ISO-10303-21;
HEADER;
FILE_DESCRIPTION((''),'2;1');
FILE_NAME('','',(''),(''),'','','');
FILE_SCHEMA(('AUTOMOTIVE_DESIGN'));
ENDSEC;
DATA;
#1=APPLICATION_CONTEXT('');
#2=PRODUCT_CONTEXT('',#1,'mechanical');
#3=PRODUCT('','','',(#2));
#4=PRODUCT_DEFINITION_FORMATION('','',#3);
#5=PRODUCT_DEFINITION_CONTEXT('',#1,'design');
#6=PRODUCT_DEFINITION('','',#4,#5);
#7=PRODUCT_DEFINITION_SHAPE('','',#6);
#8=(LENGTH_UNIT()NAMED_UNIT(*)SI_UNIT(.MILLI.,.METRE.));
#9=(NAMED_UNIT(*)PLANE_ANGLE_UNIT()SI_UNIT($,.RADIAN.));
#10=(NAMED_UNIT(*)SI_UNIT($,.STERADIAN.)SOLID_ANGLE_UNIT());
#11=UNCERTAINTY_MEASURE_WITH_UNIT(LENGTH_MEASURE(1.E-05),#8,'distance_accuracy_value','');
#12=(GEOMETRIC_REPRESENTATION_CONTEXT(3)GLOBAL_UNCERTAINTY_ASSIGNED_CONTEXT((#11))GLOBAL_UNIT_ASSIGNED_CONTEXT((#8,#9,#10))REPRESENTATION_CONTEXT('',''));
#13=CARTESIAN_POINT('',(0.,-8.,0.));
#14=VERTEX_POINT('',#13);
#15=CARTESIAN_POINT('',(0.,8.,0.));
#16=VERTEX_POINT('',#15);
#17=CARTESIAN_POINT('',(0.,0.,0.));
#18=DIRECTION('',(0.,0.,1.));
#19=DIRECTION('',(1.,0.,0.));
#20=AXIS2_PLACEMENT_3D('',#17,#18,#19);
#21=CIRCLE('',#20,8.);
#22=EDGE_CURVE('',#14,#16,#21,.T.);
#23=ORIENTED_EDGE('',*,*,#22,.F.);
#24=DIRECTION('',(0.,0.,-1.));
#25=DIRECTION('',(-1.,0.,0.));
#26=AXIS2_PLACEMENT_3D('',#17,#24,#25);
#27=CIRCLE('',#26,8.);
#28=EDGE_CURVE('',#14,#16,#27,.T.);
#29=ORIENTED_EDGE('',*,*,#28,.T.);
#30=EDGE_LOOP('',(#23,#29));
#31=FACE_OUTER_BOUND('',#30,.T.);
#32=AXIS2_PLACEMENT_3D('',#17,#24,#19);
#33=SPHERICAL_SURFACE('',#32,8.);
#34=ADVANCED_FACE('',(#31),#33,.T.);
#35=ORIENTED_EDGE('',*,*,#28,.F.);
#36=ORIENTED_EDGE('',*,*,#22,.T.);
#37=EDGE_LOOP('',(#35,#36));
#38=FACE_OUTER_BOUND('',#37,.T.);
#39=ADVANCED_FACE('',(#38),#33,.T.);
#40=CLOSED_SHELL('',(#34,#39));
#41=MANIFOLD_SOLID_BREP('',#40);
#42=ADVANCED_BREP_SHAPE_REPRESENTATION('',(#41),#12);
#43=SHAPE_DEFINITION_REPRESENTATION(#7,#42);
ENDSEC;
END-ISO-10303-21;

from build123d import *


with BuildPart() as part:
    # 草图1 → 旋转1 (revolve)
    with BuildSketch(Plane.XY):
        with BuildLine():
            Line((0, -8), (0, 8))
            ThreePointArc((0, 8), (-8, 0), (0, -8))
        make_face()
    revolve(axis=Axis((0, 8, 0), (0, -1, 0)))


solid = part.part
